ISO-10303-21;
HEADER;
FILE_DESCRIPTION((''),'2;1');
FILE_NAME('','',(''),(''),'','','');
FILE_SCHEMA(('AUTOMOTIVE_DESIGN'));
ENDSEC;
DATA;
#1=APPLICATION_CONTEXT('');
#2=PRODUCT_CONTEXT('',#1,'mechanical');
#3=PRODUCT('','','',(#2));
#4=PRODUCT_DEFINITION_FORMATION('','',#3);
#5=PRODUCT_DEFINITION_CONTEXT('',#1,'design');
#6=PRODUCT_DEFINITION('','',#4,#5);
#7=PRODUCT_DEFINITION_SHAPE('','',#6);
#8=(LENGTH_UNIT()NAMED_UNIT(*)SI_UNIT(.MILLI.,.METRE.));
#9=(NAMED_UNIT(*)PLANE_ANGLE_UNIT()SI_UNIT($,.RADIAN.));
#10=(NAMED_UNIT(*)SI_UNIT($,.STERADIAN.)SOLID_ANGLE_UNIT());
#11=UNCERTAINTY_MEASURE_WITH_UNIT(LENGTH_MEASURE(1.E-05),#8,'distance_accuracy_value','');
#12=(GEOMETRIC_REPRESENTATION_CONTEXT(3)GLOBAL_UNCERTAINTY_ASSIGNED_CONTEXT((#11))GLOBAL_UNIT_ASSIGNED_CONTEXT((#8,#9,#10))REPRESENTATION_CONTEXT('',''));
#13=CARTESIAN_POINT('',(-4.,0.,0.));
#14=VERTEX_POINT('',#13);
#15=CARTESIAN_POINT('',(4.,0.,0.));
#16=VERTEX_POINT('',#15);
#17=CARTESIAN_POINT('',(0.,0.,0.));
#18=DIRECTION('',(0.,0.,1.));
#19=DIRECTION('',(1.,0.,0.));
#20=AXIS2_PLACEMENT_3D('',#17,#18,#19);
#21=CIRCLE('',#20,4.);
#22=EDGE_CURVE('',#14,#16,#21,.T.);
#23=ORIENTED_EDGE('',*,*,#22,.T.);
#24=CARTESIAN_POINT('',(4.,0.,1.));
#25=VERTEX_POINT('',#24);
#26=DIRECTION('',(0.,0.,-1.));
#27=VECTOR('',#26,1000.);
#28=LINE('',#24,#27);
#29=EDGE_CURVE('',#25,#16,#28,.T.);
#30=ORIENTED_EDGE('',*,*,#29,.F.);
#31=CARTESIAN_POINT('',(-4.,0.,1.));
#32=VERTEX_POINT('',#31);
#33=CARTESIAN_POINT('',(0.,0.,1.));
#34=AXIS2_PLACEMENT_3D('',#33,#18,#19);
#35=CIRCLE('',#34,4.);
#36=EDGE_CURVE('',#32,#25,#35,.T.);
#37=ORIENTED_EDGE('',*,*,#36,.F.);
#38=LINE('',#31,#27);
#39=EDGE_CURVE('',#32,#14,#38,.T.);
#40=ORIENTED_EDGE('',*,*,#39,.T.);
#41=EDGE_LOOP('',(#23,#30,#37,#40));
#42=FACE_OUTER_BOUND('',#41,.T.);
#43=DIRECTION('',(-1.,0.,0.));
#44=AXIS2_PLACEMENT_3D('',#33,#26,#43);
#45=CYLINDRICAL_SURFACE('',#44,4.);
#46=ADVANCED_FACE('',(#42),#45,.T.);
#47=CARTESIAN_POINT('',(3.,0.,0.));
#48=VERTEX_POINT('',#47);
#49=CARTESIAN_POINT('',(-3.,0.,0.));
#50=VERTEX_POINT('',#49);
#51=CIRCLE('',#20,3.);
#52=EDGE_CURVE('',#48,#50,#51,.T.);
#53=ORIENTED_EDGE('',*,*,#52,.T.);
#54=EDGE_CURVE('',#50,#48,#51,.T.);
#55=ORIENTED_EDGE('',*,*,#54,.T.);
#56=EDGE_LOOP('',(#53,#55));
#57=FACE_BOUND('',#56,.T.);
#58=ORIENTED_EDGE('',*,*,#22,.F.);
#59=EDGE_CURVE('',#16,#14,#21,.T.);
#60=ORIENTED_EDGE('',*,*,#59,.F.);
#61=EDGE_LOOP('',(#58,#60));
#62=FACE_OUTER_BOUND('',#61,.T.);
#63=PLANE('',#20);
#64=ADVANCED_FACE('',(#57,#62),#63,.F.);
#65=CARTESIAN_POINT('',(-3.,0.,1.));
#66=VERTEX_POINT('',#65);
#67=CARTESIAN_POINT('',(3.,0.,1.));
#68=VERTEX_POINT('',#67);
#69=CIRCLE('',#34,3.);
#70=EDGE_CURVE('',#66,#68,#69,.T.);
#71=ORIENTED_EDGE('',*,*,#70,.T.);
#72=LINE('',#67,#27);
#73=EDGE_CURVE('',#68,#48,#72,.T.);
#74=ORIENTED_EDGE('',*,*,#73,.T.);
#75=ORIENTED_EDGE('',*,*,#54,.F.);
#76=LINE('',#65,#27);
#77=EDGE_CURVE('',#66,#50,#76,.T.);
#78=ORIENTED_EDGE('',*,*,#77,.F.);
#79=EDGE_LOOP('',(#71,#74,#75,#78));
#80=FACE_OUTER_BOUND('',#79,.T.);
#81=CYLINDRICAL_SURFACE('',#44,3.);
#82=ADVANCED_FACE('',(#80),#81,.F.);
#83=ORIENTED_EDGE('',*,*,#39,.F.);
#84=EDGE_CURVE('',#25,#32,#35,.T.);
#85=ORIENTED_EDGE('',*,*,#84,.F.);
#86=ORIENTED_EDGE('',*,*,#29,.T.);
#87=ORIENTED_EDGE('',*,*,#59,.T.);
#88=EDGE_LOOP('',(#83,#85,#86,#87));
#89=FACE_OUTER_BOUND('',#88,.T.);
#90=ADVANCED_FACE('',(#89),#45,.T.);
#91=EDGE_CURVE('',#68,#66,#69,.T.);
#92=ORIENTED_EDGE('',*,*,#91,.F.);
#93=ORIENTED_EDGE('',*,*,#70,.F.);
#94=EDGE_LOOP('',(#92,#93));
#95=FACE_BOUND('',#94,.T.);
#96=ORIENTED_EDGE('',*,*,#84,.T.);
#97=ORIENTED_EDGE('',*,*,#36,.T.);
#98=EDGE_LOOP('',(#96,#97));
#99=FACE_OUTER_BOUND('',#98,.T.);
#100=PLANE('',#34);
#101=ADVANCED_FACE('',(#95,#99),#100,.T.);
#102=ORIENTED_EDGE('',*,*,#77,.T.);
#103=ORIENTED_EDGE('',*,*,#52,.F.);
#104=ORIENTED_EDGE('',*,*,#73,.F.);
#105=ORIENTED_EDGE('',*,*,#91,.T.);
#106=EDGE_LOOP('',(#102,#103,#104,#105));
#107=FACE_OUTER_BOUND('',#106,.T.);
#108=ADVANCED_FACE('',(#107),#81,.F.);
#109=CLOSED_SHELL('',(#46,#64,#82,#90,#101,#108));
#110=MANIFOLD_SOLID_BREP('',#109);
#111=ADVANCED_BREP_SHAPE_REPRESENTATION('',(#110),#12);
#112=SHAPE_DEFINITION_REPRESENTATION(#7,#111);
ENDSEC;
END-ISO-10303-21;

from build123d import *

# Parameters (mm, degrees)
SKETCH1_R           = 4
SKETCH1_R_2         = 3
BOSS_EXTRUDE1_DEPTH = 1


with BuildPart() as part:
    # Sketch1 → Boss-Extrude1 (new body)
    with BuildSketch(Plane.XY):
        Circle(SKETCH1_R)
        Circle(SKETCH1_R_2, mode=Mode.SUBTRACT)
    extrude(amount=BOSS_EXTRUDE1_DEPTH)


solid = part.part
